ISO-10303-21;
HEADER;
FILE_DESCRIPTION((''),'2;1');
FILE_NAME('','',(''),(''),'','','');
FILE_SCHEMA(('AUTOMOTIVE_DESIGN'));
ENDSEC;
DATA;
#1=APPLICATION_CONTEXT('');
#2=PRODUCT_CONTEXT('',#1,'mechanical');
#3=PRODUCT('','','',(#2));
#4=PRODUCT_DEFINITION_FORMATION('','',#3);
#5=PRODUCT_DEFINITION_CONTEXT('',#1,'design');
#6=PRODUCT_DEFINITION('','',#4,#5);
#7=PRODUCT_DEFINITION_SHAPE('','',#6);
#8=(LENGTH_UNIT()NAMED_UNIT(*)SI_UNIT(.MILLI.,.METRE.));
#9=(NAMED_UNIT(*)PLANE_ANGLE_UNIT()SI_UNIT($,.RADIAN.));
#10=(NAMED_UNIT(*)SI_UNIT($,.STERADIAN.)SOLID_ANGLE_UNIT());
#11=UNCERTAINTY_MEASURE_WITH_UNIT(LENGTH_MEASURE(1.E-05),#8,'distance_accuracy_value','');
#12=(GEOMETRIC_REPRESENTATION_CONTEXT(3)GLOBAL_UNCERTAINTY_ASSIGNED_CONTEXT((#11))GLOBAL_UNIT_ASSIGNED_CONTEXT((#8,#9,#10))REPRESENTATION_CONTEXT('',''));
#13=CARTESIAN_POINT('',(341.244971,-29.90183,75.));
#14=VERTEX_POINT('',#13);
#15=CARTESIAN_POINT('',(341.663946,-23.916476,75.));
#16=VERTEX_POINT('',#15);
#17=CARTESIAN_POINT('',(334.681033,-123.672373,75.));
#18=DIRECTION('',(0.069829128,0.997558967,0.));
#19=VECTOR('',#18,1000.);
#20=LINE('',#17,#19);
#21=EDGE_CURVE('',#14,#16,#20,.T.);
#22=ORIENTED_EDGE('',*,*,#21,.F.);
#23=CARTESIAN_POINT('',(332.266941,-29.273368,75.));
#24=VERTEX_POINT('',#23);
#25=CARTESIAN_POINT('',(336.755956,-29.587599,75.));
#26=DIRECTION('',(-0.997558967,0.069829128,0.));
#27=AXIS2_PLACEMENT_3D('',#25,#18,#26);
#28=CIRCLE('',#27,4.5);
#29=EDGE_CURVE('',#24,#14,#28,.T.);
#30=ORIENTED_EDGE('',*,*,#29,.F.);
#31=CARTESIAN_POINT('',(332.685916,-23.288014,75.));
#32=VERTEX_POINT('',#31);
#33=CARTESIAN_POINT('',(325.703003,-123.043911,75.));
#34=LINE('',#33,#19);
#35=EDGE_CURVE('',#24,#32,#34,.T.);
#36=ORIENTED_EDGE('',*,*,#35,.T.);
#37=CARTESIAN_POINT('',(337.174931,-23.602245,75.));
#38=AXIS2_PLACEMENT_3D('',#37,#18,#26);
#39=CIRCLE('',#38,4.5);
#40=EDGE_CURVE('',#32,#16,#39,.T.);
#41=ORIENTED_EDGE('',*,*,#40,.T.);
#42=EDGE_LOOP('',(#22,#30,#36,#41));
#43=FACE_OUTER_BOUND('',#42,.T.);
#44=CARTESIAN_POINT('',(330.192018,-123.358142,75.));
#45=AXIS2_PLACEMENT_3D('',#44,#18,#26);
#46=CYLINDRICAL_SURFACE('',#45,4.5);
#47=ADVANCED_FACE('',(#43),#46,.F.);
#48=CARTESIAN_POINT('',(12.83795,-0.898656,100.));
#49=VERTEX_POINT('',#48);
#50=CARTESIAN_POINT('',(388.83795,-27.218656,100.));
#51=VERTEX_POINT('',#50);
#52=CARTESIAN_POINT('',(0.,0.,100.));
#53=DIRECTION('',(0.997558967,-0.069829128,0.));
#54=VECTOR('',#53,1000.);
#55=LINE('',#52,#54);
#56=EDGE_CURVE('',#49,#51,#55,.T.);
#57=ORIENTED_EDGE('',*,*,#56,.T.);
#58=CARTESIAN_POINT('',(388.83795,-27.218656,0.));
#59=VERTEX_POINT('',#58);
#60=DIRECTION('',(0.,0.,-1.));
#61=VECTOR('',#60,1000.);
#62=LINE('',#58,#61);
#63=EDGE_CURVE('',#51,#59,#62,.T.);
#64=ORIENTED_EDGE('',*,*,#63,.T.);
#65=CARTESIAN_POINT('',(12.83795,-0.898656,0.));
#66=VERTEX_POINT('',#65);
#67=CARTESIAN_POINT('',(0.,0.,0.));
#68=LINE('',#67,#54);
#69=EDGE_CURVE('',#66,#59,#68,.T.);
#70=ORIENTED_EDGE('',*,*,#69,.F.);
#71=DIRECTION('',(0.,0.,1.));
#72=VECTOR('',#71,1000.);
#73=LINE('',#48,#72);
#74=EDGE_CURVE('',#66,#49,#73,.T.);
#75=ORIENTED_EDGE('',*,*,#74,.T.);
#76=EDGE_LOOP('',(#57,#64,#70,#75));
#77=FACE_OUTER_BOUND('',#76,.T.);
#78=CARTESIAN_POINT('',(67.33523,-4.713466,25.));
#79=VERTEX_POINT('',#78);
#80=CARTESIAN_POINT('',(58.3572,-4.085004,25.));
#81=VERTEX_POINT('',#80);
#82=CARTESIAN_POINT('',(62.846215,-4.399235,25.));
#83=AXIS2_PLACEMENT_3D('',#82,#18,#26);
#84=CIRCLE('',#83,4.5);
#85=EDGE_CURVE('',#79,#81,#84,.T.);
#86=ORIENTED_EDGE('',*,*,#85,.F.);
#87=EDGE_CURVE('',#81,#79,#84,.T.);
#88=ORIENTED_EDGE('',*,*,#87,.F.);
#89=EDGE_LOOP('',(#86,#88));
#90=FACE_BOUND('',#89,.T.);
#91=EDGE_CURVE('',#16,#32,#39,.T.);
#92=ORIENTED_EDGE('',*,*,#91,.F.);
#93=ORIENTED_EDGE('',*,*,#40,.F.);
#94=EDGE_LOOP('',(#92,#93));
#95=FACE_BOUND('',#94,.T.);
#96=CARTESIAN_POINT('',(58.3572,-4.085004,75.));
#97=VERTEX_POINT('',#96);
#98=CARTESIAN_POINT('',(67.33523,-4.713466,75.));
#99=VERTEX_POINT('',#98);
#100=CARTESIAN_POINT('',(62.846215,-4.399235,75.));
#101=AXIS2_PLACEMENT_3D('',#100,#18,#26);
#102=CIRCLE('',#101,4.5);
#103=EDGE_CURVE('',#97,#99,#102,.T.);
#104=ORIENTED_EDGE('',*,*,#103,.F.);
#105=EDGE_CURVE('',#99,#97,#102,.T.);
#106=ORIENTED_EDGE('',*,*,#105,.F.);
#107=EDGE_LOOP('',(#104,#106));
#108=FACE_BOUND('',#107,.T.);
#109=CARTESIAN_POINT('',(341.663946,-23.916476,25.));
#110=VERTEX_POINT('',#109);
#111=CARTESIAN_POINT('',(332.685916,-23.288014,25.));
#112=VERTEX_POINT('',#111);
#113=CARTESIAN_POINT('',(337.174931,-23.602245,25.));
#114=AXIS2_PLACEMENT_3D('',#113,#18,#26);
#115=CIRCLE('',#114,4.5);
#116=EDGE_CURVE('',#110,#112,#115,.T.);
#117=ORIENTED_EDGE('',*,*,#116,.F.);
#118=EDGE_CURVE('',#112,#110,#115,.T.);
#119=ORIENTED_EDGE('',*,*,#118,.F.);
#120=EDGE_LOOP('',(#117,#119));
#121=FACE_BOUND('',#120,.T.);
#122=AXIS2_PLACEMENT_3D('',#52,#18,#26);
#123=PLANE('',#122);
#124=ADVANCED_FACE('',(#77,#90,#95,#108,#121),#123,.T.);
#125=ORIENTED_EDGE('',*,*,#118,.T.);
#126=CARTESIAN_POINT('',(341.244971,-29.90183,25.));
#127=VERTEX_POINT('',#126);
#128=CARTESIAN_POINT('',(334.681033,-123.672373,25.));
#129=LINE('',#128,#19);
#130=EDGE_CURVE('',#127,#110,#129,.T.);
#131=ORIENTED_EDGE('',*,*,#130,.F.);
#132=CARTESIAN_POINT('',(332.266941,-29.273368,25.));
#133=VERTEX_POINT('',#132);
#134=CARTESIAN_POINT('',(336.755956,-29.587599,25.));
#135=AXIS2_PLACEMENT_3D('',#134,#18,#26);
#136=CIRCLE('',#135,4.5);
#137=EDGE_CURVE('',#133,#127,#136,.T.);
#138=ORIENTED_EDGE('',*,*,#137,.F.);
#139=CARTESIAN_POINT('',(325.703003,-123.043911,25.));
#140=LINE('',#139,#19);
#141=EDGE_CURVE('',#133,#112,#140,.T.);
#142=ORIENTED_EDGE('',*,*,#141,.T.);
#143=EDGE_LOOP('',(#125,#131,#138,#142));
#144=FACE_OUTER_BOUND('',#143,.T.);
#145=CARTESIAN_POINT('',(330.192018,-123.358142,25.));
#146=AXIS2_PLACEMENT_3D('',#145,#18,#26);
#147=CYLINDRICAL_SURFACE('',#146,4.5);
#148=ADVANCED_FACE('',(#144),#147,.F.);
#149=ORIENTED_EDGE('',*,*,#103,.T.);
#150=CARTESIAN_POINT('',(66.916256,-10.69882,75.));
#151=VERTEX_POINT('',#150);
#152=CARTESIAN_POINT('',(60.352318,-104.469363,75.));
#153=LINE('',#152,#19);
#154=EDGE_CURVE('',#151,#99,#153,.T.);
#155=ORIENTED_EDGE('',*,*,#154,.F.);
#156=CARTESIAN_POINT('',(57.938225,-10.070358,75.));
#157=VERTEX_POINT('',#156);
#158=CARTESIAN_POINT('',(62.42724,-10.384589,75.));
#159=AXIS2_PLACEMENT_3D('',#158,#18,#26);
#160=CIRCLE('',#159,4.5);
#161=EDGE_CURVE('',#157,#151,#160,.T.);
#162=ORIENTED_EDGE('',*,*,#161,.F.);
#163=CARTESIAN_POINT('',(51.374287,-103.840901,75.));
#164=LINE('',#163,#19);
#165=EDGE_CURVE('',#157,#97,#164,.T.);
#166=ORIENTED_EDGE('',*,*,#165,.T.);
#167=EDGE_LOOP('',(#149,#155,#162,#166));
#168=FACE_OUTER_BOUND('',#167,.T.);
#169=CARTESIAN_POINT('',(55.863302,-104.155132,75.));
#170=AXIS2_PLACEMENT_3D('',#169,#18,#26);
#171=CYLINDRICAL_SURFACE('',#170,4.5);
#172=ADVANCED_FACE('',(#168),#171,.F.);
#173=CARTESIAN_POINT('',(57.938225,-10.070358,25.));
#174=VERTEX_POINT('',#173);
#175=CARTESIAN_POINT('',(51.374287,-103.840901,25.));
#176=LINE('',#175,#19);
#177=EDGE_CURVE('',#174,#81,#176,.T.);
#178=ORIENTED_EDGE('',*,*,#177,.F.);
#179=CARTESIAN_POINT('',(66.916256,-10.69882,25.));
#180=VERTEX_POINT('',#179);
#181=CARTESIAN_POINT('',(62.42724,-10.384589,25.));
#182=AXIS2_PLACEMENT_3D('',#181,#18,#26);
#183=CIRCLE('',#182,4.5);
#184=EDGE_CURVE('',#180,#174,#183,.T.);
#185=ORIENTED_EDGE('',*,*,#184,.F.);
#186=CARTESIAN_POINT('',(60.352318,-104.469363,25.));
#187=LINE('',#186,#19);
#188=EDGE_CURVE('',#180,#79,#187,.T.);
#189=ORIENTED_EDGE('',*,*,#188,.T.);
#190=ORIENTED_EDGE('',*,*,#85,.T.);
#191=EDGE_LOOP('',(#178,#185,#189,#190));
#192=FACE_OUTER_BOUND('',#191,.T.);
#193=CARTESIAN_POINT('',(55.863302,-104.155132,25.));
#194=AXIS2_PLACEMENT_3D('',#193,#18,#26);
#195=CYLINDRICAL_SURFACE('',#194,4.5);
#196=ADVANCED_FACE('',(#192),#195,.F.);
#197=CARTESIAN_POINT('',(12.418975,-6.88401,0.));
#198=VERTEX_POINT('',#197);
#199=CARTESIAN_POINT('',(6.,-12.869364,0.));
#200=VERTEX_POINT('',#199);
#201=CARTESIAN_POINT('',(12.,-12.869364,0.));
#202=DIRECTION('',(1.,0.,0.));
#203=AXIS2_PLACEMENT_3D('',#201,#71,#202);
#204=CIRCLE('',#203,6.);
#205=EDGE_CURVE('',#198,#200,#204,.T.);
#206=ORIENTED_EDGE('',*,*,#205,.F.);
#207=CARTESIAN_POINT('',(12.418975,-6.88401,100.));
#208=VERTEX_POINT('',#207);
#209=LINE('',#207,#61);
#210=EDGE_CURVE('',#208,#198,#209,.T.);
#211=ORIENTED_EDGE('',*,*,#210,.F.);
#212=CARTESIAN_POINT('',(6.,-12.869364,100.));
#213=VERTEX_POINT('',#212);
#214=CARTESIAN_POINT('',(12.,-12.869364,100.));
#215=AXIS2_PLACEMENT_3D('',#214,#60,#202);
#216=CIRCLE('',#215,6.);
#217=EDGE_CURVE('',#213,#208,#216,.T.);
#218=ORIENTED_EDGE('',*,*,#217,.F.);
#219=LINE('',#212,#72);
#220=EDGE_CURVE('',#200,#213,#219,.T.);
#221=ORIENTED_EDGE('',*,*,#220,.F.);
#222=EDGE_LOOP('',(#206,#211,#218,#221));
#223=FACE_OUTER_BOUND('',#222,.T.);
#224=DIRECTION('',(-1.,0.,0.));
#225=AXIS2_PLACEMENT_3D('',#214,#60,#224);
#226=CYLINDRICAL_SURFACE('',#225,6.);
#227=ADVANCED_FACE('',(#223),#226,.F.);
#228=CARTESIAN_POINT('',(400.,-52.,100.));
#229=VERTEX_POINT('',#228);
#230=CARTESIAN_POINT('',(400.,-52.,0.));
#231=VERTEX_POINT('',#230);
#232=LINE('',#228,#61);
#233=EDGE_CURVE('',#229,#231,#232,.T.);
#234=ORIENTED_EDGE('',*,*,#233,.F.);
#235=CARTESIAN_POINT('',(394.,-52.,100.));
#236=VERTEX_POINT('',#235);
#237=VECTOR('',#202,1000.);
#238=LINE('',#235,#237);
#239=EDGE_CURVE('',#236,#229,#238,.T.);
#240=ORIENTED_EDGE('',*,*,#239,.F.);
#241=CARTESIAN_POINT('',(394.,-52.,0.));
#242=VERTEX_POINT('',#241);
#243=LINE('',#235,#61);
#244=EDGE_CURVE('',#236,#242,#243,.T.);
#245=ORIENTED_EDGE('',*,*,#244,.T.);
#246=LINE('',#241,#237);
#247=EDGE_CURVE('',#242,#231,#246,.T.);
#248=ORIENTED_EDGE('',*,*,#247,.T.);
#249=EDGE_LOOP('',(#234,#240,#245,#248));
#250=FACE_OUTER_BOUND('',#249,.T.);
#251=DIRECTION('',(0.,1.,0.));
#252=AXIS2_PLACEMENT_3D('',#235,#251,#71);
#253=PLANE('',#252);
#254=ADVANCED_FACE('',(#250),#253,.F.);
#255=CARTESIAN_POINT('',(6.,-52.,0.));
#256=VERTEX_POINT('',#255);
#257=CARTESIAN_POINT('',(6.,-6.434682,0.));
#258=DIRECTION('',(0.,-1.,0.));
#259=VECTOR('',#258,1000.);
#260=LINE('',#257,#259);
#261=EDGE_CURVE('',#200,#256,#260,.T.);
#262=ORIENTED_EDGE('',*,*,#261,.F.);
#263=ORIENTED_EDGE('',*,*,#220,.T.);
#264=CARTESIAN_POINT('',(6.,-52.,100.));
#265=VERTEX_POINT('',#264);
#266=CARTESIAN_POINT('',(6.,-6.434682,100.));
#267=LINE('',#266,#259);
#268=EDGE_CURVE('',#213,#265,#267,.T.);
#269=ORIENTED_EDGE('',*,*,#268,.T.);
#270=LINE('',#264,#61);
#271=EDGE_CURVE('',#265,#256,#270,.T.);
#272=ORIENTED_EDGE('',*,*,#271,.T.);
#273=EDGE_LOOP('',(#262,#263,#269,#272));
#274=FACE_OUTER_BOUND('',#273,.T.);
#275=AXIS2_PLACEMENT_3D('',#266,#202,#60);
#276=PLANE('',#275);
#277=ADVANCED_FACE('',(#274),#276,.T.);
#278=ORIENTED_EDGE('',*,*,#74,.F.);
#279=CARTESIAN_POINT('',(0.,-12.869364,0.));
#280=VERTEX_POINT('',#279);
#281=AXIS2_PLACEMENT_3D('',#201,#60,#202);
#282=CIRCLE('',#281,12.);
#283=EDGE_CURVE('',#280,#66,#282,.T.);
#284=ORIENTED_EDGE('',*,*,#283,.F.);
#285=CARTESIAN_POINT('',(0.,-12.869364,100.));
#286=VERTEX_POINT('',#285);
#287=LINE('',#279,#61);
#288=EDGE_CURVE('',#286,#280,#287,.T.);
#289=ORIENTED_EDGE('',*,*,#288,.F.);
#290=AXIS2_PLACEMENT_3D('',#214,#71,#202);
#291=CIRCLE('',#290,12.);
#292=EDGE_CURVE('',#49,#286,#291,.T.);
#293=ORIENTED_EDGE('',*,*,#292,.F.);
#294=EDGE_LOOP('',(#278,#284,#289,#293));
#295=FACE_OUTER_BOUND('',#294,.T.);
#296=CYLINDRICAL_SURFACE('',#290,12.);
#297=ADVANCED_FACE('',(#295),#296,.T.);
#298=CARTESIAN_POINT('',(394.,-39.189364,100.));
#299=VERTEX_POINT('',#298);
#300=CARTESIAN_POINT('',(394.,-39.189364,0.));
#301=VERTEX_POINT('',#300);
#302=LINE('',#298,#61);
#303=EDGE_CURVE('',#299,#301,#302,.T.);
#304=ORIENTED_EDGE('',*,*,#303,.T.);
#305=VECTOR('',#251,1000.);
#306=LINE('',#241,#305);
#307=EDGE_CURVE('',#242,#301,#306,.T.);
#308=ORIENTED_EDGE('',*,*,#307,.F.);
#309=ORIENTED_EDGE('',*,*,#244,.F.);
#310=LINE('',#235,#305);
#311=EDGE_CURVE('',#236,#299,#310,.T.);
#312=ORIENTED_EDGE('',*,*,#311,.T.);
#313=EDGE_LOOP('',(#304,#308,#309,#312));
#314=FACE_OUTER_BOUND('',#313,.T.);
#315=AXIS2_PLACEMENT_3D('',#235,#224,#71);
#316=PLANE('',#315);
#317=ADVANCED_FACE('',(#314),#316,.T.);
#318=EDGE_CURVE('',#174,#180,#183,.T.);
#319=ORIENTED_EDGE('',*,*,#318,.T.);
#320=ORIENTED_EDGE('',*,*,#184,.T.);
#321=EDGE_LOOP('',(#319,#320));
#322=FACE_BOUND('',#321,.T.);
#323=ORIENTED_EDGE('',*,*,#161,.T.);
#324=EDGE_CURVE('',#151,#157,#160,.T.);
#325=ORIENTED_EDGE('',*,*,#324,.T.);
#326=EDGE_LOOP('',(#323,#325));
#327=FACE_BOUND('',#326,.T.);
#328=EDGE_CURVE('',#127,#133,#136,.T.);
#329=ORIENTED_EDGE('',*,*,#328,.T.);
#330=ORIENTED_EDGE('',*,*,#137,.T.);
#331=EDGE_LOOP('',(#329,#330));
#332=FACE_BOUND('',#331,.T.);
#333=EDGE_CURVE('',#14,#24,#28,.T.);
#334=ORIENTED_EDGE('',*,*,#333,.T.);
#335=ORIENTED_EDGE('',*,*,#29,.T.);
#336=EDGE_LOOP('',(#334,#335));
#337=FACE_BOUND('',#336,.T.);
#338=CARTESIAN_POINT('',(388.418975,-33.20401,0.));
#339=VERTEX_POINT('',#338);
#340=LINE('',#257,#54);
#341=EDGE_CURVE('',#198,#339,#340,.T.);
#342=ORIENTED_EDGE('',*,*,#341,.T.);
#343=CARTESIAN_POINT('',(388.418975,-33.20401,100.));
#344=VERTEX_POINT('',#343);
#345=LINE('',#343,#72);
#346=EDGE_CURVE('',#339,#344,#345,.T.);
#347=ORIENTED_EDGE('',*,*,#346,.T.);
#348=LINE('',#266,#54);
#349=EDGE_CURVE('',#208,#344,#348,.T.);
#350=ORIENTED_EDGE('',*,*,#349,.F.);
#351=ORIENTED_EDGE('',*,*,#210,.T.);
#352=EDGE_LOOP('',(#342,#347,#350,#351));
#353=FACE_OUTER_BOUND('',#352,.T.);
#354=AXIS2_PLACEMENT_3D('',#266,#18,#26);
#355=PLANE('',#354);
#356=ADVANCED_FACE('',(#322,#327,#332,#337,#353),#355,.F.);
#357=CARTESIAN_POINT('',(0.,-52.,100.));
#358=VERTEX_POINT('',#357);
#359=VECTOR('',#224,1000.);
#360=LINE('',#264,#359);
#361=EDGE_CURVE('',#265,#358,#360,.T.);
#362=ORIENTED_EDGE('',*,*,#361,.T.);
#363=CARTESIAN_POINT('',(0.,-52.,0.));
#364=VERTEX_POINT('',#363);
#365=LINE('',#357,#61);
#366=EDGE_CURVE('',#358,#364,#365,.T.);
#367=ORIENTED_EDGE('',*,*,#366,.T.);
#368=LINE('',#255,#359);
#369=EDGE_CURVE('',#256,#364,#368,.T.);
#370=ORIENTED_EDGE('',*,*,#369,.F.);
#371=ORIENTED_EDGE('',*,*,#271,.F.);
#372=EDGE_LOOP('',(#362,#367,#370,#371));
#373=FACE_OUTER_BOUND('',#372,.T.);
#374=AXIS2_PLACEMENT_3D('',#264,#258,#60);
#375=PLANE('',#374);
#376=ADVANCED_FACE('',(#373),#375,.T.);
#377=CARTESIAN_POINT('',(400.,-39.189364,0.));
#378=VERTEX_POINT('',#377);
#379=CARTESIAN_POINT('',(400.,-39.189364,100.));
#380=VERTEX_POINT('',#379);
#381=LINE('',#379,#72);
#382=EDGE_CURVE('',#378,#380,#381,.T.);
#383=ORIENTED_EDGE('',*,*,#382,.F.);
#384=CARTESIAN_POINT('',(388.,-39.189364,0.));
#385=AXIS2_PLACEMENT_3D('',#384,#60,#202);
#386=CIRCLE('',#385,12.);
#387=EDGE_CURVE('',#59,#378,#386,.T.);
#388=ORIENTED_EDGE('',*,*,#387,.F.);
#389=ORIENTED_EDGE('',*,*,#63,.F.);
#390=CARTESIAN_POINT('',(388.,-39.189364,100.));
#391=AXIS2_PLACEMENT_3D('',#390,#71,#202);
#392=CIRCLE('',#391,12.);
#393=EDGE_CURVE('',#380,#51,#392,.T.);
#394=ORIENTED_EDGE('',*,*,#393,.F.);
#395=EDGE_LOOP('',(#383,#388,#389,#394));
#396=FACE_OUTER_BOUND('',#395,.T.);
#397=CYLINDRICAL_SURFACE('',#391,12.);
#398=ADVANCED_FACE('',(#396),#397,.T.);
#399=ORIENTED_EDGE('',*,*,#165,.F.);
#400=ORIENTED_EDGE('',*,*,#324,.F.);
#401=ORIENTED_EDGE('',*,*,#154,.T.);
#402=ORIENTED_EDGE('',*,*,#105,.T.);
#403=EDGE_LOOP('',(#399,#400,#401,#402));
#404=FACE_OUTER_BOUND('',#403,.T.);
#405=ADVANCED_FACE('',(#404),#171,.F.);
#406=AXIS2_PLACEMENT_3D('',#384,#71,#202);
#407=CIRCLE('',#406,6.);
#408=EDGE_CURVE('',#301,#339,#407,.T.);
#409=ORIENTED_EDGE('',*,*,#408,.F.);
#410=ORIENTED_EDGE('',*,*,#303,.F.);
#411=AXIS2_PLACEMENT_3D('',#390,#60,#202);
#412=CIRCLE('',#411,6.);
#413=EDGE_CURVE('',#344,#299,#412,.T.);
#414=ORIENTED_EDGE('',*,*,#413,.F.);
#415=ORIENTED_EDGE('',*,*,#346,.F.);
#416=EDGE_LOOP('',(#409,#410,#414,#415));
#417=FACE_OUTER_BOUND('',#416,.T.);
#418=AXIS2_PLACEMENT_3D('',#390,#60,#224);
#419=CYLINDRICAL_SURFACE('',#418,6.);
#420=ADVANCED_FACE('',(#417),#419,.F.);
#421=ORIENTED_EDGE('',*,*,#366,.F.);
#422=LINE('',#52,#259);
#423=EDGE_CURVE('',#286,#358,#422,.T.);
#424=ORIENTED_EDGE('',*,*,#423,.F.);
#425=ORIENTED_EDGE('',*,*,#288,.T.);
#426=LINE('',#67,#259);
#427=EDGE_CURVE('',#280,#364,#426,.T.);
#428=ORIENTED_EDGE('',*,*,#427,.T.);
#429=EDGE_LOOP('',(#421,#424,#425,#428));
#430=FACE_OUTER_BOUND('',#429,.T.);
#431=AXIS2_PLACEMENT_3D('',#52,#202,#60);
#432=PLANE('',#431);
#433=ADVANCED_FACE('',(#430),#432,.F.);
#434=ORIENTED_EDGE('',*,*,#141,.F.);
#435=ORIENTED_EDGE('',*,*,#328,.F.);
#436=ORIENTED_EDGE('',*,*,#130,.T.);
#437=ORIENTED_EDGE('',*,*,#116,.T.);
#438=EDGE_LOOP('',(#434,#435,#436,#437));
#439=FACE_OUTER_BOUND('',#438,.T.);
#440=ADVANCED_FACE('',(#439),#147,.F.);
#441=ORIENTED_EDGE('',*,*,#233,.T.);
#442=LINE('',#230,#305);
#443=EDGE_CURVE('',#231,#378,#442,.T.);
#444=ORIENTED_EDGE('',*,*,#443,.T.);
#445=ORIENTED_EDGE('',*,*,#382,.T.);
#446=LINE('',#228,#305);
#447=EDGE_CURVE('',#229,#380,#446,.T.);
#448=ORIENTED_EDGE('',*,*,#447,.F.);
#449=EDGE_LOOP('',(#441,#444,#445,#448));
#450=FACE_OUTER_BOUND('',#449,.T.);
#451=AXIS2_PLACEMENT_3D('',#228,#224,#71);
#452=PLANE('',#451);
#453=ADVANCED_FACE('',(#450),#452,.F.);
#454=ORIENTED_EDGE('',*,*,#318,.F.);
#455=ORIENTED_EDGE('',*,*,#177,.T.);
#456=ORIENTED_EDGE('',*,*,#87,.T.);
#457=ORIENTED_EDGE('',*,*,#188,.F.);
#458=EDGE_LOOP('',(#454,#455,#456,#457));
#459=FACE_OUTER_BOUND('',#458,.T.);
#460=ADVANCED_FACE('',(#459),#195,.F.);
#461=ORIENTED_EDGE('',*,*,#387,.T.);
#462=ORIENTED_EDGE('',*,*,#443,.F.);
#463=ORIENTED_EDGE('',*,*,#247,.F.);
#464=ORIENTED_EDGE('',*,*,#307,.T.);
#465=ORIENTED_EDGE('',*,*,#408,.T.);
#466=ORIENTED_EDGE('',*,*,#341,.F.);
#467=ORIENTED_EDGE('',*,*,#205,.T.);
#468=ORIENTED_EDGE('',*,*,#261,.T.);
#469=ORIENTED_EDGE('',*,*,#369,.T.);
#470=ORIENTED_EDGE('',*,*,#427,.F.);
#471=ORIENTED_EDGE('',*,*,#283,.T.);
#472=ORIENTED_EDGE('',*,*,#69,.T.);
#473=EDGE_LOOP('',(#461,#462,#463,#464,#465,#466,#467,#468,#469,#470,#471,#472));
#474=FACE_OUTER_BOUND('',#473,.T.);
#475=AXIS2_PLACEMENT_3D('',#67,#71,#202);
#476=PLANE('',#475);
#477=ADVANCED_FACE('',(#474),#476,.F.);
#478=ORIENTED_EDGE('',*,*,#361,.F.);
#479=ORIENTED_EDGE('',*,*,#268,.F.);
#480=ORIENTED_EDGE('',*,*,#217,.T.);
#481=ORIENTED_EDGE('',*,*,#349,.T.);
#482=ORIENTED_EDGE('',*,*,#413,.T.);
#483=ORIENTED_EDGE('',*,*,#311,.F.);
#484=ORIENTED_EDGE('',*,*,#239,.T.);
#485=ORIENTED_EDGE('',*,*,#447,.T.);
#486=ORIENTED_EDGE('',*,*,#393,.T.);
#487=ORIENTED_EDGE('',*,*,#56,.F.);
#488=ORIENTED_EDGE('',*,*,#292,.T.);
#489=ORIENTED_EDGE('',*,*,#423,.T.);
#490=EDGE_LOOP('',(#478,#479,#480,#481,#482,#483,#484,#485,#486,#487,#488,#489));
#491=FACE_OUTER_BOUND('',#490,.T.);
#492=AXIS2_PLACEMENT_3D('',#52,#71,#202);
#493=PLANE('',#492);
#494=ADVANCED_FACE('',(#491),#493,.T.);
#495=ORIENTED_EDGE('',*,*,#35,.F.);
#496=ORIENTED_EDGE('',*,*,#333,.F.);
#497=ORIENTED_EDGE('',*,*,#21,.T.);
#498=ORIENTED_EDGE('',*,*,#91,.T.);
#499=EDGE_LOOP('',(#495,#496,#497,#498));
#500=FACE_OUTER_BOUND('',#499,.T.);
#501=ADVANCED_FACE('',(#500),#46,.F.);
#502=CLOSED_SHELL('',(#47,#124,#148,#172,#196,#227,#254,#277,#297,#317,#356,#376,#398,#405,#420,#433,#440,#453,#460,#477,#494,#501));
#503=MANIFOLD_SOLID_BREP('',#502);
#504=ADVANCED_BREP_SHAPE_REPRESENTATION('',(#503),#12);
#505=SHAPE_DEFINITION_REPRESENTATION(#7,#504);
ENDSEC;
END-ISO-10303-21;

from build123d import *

# Parameters (mm, degrees)
BOSS_EXTRUDE1_DEPTH = 100
SKETCH4_R           = 4.5
CUT_EXTRUDE2_DEPTH  = 100
FILLET1_R           = 12
FILLET2_R           = 6


with BuildPart() as part:
    # Sketch1 → Boss-Extrude1 (new body)
    with BuildSketch(Plane.XY):
        Polygon((0, 0), (0, -52), (6, -52), (6, -6.434682036), (394, -33.594682036), (394, -52), (400, -52), (400, -28), align=None)
    extrude(amount=BOSS_EXTRUDE1_DEPTH)

    # Sketch4 → Cut-Extrude2 (cut)
    with BuildSketch(Plane(origin=(0, 0, 0), x_dir=(0.9975589671416267, -0.06982912769991385, 0), z_dir=(0.06982912769991385, 0.9975589671416267, 0))):
        with Locations(Location((63, -25, 0), (0, 0, 180))):
            Circle(SKETCH4_R)
        with Locations(Location((338, -25, 0), (0, 0, 180))):
            Circle(SKETCH4_R)
        with Locations(Location((63, -75, 0), (0, 0, 180))):
            Circle(SKETCH4_R)
        with Locations(Location((338, -75, 0), (0, 0, 180))):
            Circle(SKETCH4_R)
    extrude(amount=-CUT_EXTRUDE2_DEPTH, mode=Mode.SUBTRACT)

    # Fillet1
    fillet1_edges = [part.edges().sort_by_distance(p)[0] for p in [
        (400, -28, 50),
        (0, 0, 50),
    ]]
    fillet(fillet1_edges, radius=FILLET1_R)

    # Fillet2
    fillet2_edges = [part.edges().sort_by_distance(p)[0] for p in [
        (6, -6.434682036, 50),
        (394, -33.594682036, 50),
    ]]
    fillet(fillet2_edges, radius=FILLET2_R)


solid = part.part
